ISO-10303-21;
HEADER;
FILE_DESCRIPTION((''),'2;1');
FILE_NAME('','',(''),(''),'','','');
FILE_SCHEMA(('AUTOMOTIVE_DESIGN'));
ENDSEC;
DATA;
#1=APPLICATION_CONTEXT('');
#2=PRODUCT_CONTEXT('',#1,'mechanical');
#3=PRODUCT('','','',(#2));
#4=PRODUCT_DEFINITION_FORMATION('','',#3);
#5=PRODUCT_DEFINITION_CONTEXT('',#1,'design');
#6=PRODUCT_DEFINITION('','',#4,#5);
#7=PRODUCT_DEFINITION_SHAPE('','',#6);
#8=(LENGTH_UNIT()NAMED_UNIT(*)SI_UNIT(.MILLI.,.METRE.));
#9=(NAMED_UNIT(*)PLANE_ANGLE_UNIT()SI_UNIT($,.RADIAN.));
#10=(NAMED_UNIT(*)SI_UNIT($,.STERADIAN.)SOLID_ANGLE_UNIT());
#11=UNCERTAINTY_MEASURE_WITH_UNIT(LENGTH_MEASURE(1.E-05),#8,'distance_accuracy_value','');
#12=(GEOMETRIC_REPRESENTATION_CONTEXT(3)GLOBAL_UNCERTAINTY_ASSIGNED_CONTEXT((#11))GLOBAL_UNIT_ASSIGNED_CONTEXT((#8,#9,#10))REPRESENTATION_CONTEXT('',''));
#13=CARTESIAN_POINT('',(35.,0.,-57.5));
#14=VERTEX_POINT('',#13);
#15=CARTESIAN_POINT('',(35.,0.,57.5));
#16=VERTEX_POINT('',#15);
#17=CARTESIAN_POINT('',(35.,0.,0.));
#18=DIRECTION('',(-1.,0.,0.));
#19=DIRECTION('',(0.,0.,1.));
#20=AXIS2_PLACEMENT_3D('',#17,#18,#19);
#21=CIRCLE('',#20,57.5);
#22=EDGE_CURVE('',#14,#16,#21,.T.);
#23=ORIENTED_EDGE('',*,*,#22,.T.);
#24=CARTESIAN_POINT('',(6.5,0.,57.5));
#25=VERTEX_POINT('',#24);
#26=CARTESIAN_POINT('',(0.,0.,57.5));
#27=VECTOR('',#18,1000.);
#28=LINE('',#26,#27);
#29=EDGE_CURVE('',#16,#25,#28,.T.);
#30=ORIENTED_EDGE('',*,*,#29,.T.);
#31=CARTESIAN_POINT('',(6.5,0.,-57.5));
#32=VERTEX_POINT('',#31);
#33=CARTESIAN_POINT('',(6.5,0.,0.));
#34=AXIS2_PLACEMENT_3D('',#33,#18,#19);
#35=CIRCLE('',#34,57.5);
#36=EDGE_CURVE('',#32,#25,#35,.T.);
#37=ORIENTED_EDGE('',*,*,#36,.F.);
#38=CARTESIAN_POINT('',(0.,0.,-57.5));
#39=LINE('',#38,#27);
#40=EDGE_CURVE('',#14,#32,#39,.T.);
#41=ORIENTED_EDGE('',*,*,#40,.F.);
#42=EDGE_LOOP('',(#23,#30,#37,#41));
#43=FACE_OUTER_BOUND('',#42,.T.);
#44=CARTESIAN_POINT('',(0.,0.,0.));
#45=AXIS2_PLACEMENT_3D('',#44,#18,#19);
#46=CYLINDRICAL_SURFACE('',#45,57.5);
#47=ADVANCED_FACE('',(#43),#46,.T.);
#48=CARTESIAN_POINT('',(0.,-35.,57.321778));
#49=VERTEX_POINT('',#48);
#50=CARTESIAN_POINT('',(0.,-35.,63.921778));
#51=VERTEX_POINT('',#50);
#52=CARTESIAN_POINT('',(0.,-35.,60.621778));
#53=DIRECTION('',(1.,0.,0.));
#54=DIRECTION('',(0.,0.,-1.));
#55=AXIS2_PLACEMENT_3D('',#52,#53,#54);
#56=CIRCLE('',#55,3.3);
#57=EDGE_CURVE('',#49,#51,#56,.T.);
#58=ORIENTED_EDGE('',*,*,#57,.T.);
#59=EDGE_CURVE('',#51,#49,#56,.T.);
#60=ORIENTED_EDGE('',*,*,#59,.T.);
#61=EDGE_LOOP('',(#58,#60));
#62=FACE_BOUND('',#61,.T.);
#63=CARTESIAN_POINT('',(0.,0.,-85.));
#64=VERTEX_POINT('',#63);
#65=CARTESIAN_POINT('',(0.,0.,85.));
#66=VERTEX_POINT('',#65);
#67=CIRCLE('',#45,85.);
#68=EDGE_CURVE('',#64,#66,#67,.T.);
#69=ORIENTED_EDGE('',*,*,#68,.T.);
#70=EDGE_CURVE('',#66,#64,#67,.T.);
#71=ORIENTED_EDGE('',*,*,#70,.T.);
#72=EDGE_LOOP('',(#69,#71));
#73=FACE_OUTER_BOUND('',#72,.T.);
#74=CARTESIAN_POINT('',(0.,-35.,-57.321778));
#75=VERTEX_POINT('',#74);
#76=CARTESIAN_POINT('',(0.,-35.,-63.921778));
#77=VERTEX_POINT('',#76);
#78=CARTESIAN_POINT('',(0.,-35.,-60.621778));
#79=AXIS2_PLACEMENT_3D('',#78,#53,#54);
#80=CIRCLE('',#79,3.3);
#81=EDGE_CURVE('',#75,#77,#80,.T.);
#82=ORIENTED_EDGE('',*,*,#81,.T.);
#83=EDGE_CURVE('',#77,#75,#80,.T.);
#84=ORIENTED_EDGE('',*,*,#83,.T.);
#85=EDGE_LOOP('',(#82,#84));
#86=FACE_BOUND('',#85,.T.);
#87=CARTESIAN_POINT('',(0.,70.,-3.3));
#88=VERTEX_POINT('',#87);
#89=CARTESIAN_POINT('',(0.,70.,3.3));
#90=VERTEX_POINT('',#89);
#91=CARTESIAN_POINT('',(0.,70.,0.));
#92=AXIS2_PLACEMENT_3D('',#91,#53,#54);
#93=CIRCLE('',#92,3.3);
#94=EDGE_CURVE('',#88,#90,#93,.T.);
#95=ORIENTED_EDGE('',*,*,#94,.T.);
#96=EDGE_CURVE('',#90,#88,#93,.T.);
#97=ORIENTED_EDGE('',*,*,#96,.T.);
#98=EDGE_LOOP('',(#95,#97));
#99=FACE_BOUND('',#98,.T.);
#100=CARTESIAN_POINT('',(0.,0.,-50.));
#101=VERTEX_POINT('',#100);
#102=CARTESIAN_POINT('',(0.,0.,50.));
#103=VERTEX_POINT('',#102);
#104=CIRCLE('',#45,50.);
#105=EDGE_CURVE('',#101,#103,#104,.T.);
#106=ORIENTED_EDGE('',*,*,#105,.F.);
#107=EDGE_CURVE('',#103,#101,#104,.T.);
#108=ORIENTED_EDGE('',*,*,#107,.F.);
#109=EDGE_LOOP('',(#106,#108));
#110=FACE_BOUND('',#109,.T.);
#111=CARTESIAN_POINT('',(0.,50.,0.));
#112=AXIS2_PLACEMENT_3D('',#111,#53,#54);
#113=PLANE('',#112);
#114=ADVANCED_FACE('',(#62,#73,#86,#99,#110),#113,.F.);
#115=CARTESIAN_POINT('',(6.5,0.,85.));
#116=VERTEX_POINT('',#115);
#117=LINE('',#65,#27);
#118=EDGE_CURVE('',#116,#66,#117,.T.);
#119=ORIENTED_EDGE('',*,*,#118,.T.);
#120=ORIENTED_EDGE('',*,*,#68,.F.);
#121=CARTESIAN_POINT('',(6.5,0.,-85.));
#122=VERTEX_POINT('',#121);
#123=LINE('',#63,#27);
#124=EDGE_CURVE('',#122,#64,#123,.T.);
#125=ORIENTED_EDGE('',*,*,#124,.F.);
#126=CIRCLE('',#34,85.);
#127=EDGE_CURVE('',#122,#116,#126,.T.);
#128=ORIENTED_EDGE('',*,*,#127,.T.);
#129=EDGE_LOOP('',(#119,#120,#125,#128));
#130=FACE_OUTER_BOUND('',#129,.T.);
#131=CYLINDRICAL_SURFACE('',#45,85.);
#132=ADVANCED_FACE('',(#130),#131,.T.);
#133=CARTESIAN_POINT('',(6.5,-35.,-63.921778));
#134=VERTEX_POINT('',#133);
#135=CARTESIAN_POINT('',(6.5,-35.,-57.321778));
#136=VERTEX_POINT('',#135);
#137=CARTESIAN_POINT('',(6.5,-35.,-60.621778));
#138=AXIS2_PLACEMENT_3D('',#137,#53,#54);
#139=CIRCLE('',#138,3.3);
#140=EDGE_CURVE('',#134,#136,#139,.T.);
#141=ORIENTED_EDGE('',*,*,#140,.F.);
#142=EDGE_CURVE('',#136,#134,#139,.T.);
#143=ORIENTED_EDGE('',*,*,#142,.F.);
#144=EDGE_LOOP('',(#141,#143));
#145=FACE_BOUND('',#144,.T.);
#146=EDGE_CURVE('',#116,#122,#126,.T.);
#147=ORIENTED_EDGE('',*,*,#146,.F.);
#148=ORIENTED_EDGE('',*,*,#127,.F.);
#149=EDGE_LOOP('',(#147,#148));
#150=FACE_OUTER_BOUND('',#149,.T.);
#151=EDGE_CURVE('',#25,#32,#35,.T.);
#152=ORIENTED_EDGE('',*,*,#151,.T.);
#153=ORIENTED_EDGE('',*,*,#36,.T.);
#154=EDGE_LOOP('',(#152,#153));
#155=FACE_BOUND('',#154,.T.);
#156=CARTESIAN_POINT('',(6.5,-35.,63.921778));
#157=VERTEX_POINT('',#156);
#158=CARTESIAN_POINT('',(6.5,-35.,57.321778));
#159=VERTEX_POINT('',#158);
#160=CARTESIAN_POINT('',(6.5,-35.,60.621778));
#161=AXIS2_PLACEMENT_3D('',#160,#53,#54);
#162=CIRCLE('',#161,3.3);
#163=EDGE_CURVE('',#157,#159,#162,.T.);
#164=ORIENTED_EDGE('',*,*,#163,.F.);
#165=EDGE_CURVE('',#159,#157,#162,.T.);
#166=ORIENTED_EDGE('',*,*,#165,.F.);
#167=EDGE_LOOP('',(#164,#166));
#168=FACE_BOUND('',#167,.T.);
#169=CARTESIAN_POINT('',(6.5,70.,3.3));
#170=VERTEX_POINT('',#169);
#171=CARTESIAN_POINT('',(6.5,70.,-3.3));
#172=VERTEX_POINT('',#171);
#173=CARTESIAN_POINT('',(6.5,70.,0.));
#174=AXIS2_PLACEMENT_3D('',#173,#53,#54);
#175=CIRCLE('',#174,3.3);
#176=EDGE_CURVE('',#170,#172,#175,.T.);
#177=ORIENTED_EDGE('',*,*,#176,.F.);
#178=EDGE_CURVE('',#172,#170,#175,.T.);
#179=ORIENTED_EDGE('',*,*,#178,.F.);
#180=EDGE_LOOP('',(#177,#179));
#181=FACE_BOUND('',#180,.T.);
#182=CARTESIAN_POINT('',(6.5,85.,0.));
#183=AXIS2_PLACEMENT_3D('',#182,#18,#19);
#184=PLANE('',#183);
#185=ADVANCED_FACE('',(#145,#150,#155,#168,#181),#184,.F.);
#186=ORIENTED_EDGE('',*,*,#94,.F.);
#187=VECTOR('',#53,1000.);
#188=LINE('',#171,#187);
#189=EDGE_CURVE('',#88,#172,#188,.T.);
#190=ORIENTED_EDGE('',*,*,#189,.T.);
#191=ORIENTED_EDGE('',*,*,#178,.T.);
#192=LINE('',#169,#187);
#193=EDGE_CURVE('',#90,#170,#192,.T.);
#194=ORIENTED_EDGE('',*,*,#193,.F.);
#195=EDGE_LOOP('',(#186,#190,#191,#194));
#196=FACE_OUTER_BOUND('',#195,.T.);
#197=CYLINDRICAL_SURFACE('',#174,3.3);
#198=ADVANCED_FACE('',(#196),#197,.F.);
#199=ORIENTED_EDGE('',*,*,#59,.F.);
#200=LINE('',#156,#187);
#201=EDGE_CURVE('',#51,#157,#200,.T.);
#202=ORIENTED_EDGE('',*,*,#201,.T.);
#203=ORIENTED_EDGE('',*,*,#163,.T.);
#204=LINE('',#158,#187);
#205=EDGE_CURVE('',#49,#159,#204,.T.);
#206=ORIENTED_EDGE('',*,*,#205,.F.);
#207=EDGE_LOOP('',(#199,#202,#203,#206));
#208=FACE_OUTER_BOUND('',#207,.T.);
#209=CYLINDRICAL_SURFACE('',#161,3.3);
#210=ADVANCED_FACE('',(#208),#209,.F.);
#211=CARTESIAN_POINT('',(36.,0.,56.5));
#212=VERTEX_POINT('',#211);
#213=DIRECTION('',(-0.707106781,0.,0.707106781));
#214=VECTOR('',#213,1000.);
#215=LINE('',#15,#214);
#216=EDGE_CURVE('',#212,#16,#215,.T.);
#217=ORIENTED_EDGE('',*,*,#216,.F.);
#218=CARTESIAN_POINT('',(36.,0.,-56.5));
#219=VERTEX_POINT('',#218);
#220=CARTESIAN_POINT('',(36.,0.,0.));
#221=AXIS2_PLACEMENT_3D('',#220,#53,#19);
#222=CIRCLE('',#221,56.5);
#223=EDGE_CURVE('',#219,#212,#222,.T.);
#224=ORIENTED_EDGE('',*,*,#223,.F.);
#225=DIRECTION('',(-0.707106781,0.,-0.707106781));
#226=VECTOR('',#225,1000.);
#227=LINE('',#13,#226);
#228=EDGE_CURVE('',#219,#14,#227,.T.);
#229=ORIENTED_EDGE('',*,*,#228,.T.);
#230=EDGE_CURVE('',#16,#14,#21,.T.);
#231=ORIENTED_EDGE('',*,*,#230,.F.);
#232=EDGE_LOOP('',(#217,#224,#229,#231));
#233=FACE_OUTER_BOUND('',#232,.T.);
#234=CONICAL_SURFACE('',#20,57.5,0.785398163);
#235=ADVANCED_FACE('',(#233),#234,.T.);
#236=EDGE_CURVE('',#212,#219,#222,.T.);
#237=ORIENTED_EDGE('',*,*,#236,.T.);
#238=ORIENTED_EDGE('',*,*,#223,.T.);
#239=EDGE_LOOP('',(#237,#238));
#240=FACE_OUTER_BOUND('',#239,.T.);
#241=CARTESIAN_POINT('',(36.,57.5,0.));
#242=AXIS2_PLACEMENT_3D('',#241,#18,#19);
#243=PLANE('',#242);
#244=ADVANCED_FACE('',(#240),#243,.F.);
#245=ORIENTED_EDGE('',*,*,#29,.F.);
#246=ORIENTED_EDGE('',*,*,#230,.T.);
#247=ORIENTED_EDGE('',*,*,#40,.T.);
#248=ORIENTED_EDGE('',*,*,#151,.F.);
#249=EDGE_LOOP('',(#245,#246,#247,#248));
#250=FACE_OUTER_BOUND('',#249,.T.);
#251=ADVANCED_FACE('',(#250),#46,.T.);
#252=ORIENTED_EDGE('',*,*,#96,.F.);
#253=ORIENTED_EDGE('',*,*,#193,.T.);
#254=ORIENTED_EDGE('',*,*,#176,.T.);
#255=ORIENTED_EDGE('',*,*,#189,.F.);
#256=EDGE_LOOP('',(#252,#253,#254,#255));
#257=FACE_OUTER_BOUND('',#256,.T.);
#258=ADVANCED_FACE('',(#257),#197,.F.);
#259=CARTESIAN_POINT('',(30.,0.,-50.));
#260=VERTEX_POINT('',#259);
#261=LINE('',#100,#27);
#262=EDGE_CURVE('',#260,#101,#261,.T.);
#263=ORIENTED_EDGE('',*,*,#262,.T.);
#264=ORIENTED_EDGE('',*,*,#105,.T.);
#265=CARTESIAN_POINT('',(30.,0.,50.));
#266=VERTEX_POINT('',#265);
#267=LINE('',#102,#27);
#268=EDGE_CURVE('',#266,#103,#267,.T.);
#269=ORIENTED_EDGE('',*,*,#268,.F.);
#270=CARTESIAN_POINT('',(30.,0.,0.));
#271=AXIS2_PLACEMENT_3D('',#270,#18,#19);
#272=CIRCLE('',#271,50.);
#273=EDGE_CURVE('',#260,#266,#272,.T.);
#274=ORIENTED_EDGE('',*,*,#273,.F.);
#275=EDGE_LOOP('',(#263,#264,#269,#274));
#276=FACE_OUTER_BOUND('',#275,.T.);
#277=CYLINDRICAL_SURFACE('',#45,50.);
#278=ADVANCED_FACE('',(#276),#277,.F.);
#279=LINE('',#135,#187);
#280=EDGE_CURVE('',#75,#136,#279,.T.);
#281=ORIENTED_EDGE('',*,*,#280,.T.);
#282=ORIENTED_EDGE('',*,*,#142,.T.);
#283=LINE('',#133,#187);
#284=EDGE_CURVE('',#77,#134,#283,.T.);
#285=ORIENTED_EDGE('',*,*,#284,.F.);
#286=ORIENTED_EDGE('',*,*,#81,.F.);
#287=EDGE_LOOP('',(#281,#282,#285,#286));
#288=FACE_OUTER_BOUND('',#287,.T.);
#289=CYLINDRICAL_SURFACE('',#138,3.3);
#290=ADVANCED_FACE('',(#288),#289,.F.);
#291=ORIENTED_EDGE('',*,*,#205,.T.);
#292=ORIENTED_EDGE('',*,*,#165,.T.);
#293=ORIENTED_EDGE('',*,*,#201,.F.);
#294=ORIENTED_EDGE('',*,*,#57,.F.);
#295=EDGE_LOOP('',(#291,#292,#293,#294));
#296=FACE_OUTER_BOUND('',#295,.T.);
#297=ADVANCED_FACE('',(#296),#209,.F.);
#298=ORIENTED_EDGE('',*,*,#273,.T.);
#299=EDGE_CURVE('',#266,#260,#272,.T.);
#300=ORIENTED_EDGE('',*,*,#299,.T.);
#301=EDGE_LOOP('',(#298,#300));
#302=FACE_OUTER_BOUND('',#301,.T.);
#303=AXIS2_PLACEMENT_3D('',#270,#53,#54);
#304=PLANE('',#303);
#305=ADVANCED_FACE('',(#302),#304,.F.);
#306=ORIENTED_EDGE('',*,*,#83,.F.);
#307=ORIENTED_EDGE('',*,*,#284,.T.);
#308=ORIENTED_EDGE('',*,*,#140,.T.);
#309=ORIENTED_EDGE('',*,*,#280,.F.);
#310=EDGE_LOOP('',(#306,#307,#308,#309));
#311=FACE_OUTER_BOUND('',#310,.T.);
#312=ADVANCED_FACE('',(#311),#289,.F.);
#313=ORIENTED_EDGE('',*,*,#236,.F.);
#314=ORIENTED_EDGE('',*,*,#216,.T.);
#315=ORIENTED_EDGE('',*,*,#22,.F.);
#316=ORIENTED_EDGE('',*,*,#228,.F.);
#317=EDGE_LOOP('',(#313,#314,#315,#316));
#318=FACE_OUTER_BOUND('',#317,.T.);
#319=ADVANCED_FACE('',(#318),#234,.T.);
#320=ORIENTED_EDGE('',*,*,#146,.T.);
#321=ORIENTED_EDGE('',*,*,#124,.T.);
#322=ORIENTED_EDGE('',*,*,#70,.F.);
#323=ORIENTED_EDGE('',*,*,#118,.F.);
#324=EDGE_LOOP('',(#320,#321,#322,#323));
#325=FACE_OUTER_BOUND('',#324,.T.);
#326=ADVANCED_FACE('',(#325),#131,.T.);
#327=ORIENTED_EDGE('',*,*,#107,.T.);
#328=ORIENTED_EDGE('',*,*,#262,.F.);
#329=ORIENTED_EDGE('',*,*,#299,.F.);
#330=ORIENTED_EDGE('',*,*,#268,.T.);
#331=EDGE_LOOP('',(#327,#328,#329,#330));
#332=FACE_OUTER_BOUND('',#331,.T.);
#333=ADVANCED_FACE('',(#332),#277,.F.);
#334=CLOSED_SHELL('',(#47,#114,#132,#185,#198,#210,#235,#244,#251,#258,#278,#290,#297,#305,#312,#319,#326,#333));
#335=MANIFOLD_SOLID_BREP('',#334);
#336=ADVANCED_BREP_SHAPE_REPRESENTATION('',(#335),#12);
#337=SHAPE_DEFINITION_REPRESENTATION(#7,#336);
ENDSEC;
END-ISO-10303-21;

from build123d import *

# Parameters (mm, degrees)
HOLE_WIZARD_M6_1_D = 6.6
CHAMFER_1_SIZE     = 1


with BuildPart() as part:
    # 草图2 → 旋转1 (revolve)
    with BuildSketch(Plane.XY, mode=Mode.PRIVATE) as revolve_1_sk:
        Polygon((30, 0), (30, 50), (0, 50), (0, 85), (6.5, 85), (6.5, 57.5), (36, 57.5), (36, 0), align=None)
    revolve(revolve_1_sk.sketch.rotate(Axis((0, 0, 0), (1, 0, 0)), 90), axis=Axis((0, 0, 0), (1, 0, 0)))

    # M6 间隙孔1 (through all)
    with Locations(Plane(origin=(6.5, 0, 0), x_dir=(0, 0, -1), z_dir=(1, 0, 0))):
        with Locations((-60.621778265, -35), (0, 70), (60.621778265, -35)):
            Hole(HOLE_WIZARD_M6_1_D / 2)

    # 倒角1
    chamfer_1_edges = [part.edges().sort_by_distance(p)[0] for p in [
        (36, 0, -57.5),
    ]]
    chamfer(chamfer_1_edges, length=CHAMFER_1_SIZE)


solid = part.part
